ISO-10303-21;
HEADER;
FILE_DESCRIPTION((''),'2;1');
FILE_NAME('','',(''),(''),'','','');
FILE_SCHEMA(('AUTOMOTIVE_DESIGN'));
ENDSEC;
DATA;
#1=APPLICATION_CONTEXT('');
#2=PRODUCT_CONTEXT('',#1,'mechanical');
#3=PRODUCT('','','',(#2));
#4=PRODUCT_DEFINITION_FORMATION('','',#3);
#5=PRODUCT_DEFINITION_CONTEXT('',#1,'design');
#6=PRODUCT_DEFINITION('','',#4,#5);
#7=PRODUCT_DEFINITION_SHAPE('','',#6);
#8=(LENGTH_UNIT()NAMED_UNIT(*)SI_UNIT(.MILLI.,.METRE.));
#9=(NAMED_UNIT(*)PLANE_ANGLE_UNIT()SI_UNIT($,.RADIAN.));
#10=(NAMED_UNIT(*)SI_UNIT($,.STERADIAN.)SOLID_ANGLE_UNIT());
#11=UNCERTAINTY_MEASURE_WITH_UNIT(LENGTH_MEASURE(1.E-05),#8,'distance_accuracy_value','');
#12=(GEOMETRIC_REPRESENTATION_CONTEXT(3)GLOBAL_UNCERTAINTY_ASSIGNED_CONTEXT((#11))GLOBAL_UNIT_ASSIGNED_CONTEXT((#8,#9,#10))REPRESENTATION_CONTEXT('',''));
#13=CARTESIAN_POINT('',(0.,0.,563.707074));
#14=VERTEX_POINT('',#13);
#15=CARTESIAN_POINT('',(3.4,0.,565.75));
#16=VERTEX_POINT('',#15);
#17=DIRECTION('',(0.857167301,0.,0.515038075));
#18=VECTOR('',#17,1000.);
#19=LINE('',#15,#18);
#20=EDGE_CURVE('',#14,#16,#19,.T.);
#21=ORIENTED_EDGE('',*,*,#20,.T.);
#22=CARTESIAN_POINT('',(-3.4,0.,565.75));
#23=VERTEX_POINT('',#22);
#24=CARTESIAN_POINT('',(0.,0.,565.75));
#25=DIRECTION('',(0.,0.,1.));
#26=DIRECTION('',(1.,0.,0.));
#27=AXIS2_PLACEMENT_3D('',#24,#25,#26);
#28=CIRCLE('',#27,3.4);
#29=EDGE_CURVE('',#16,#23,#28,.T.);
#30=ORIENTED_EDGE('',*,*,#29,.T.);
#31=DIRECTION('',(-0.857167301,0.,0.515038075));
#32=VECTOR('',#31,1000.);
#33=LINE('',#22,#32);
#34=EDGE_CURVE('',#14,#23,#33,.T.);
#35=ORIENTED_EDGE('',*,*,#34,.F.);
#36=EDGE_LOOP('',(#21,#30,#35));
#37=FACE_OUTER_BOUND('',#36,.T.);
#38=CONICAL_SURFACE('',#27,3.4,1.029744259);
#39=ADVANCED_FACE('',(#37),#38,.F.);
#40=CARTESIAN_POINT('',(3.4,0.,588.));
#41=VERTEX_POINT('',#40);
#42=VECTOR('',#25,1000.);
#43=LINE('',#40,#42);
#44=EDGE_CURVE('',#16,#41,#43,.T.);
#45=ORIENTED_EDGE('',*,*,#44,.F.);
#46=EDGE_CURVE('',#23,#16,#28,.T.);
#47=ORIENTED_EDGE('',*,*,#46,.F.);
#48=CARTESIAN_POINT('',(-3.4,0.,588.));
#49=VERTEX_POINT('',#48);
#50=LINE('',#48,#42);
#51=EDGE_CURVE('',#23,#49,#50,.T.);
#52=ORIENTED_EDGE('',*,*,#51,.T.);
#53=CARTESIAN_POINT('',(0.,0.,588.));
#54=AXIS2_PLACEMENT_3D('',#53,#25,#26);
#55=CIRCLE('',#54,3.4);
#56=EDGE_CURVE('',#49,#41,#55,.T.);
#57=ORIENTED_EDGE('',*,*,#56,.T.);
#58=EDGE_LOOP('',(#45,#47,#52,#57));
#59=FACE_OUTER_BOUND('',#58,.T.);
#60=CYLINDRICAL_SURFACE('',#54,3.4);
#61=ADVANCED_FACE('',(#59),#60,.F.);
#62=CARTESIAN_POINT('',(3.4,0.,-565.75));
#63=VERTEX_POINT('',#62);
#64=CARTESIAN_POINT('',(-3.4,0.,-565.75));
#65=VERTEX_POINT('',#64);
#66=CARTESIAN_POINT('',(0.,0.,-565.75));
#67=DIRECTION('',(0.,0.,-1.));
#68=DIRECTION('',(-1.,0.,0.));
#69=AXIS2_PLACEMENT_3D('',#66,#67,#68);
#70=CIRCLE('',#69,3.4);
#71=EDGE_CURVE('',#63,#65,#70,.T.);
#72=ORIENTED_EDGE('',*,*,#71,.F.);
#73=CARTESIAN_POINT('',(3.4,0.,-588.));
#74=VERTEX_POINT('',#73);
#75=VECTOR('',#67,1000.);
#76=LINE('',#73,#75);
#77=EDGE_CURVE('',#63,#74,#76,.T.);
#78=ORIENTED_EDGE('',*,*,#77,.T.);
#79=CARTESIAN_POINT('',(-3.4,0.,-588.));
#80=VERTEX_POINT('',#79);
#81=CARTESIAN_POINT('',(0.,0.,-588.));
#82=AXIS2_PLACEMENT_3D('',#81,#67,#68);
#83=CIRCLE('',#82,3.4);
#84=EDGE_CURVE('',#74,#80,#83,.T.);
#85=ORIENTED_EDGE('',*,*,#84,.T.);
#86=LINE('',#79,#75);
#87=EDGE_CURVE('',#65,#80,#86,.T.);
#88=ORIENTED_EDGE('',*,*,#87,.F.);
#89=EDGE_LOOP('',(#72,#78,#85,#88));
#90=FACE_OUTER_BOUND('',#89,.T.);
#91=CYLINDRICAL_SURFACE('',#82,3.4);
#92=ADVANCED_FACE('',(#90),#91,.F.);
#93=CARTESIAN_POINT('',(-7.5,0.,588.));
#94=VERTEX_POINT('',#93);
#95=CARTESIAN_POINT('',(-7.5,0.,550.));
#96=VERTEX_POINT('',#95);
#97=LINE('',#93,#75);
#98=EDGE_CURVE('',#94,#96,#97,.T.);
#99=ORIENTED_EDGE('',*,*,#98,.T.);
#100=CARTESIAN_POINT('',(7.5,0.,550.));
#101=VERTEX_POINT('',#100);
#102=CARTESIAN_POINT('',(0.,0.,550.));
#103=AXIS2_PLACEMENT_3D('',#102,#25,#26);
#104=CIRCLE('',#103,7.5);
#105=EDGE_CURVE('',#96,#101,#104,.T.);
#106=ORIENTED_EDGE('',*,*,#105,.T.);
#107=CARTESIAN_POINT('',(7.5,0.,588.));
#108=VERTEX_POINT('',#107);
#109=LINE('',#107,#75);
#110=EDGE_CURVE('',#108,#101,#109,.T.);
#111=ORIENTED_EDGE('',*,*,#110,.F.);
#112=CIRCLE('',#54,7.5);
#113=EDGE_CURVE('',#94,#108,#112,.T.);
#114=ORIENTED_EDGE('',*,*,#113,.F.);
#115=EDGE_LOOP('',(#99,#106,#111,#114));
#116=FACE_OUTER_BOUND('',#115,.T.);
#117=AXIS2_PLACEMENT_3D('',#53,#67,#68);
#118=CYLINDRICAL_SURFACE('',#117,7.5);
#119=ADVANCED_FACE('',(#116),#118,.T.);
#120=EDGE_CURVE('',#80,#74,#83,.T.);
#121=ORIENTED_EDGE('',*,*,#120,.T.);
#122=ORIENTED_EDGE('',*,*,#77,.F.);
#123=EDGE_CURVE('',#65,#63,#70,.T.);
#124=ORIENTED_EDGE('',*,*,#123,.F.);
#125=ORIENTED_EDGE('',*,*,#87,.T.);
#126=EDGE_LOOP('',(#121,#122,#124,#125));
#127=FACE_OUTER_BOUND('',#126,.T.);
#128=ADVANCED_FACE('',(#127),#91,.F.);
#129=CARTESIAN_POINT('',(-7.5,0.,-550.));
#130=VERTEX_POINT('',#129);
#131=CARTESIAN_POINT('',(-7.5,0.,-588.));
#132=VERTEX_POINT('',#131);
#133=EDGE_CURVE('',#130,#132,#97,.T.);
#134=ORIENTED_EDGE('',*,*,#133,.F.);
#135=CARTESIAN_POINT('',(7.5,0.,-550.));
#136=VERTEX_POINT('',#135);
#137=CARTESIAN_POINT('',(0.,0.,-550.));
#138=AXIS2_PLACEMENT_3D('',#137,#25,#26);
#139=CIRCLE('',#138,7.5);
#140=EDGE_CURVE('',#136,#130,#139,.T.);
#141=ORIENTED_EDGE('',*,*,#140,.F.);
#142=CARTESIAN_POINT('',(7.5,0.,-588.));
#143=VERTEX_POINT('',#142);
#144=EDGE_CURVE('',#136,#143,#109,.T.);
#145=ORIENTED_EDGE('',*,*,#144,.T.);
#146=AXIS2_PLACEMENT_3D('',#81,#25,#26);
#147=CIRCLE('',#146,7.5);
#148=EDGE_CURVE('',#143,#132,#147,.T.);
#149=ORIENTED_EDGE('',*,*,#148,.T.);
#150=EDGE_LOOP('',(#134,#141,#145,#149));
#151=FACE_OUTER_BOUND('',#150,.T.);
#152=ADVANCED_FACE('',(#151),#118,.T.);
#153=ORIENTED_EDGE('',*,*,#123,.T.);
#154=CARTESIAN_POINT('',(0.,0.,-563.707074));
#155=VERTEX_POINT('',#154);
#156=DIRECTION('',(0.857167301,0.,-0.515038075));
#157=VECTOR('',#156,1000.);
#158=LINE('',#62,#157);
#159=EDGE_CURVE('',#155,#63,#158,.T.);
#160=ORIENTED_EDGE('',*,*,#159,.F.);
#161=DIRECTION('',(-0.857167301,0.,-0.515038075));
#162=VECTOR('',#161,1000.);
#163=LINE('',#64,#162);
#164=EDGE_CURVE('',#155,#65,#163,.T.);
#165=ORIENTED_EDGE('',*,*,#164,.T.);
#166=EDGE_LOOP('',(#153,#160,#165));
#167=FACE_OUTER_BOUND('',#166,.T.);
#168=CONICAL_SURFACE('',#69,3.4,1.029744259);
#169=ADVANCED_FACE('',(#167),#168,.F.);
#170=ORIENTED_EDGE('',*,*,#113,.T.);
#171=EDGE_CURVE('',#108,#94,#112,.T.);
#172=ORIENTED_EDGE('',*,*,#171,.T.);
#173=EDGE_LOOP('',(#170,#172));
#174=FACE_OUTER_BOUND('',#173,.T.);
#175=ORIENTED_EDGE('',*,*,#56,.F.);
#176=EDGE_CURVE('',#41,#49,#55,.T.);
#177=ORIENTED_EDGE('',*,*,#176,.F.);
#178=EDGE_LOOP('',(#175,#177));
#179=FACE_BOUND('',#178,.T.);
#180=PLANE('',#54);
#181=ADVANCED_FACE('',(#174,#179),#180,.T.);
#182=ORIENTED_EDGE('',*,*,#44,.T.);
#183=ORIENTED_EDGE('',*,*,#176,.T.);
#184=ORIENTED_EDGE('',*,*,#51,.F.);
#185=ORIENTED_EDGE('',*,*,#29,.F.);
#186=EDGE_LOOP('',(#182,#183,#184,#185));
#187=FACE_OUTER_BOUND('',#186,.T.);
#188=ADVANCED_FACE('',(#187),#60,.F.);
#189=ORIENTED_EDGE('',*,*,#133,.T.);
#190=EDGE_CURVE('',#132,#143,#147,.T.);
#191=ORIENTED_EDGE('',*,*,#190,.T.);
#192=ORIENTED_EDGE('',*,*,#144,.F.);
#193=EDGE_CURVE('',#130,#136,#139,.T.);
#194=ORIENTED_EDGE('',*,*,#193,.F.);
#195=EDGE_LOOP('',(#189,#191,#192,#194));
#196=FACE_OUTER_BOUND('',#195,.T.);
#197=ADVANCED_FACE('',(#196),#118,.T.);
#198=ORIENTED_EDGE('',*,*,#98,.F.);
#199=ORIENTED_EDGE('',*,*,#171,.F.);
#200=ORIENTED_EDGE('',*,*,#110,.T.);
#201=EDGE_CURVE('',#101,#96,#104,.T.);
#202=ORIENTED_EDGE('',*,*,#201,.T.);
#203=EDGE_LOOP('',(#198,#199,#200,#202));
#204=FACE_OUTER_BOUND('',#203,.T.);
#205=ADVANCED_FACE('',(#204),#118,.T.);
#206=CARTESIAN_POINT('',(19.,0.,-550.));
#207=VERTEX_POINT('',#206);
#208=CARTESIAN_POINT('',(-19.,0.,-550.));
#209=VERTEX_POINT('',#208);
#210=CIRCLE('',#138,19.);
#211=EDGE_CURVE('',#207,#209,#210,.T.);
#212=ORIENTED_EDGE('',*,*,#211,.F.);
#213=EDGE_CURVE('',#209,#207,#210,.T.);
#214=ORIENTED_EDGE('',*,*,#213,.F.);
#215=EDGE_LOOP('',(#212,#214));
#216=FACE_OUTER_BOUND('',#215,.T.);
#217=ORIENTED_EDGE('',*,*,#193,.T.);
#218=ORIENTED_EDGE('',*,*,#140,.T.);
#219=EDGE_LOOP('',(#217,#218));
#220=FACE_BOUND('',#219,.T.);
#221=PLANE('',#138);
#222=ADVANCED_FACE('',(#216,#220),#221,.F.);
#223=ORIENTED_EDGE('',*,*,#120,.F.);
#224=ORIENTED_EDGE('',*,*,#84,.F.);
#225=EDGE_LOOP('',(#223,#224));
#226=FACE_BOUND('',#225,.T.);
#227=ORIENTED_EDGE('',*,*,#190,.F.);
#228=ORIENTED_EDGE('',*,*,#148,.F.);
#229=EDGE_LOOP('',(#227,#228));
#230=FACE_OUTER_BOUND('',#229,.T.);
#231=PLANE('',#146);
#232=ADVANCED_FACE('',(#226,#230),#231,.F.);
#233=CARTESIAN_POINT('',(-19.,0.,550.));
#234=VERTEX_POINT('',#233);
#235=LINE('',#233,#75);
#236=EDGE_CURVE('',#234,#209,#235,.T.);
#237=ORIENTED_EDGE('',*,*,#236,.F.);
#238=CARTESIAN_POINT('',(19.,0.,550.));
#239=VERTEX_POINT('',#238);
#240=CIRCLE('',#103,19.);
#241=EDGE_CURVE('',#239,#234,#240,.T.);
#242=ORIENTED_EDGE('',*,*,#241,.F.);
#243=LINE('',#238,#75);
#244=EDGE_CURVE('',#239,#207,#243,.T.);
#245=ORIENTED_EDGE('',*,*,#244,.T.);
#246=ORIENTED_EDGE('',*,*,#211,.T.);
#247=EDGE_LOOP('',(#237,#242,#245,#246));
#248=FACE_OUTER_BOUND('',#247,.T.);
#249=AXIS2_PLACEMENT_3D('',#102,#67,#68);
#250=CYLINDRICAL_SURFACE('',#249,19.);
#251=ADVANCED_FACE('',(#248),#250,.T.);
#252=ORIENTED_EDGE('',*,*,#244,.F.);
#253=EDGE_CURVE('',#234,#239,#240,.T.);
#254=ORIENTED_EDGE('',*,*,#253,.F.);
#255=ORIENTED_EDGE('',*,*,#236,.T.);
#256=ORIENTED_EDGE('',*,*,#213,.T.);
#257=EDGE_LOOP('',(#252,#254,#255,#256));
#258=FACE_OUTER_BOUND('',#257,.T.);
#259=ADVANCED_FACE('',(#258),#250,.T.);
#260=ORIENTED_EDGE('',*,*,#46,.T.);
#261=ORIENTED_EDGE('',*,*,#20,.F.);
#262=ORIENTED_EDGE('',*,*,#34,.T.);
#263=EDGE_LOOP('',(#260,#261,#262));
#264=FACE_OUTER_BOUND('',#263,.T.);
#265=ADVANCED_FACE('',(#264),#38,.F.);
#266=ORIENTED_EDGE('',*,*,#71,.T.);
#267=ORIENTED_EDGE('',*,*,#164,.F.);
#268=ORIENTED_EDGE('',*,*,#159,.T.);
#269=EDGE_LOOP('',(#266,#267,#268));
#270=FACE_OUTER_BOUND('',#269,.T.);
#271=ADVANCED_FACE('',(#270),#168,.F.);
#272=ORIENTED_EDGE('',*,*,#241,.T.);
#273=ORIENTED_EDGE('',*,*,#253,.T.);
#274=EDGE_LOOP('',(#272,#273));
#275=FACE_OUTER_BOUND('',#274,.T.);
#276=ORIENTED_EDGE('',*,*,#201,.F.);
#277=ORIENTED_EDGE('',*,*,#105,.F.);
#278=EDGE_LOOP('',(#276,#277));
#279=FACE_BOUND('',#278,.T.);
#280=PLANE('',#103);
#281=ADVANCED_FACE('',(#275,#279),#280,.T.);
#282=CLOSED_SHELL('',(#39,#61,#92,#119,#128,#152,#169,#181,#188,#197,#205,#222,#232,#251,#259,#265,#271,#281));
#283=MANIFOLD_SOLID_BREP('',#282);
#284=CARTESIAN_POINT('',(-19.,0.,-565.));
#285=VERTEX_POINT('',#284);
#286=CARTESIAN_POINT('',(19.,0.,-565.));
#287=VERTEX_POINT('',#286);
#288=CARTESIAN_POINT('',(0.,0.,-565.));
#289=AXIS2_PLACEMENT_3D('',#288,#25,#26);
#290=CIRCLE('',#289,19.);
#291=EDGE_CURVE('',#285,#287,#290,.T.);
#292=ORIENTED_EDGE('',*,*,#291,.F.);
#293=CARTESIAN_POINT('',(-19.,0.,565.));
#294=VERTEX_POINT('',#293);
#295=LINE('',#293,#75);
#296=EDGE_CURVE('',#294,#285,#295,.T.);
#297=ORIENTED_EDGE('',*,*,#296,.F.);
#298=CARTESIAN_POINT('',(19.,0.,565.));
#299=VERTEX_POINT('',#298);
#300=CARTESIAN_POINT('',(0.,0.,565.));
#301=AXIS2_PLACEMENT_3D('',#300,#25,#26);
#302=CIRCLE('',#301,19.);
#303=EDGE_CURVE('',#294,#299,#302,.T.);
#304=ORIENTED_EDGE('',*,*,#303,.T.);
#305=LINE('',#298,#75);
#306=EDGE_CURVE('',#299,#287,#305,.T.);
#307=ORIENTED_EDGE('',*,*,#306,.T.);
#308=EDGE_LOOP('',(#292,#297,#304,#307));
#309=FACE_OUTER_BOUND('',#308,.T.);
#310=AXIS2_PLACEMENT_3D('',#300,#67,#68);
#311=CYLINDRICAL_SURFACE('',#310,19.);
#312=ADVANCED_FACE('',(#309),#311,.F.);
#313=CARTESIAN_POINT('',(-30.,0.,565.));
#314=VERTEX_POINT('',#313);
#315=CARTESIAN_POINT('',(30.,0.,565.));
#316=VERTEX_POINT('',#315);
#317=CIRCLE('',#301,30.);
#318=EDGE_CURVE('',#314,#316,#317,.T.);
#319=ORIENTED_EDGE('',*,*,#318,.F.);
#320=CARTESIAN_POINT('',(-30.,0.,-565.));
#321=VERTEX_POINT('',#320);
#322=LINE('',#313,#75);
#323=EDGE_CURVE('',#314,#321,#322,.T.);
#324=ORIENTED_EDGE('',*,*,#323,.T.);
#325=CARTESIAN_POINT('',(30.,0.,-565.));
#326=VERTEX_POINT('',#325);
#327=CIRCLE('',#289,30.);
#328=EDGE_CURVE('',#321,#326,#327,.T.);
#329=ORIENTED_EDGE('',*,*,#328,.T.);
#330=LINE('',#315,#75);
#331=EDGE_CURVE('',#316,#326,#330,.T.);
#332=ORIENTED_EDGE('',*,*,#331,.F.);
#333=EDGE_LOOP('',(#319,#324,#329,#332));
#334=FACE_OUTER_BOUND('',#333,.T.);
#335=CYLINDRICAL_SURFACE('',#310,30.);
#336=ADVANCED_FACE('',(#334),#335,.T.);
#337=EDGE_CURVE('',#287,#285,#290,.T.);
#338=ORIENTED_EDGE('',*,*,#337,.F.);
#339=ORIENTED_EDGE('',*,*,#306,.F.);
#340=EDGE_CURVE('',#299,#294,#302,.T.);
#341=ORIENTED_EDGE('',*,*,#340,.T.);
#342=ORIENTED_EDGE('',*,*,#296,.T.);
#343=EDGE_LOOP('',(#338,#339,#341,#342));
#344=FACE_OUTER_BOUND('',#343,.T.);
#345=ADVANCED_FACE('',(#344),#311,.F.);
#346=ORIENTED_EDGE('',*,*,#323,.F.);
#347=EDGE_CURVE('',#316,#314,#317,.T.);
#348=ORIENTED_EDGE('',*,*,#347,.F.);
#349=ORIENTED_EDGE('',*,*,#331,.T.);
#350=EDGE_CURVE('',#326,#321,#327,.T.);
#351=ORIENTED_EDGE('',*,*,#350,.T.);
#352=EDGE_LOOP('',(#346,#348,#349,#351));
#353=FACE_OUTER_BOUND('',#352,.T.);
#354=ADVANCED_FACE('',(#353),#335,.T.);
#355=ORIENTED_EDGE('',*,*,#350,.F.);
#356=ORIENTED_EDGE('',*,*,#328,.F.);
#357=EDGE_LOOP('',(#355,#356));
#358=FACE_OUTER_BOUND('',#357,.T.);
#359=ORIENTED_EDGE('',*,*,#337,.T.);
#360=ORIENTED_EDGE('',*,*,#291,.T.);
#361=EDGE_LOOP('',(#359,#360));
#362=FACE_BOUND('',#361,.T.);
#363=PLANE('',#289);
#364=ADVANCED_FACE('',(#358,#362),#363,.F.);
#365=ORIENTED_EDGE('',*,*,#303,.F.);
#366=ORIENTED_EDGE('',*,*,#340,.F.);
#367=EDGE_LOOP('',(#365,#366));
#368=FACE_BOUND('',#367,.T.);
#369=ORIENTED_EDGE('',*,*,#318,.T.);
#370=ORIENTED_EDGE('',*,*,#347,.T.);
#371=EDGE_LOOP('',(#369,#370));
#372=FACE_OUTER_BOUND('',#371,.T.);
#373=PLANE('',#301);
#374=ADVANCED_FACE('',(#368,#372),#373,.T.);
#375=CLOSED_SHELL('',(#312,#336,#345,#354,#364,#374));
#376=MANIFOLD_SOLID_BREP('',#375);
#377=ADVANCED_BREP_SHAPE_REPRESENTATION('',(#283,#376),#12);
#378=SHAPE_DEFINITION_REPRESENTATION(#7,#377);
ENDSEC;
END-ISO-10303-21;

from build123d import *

# Parameters (mm, degrees)
SKETCH_1_R      = 7.5
EXTRUDE_1_DEPTH = 588
SKETCH_2_R      = 19
EXTRUDE_2_DEPTH = 550
SKETCH_3_R      = 30
SKETCH_3_R_2    = 19
EXTRUDE_3_DEPTH = 565


with BuildPart() as part:
    # 草图1 → 凸台-拉伸1 (new, symmetric)
    with BuildSketch(Plane.XY):
        Circle(SKETCH_1_R)
    extrude(amount=EXTRUDE_1_DEPTH, both=True)

    # 草图2 → 凸台-拉伸2 (add, symmetric)
    with BuildSketch(Plane.XY):
        Circle(SKETCH_2_R)
    extrude(amount=EXTRUDE_2_DEPTH, both=True)

    # 草图5 → M8 螺纹孔1 (revolve, cut)
    with BuildSketch(Plane(origin=(0, 0, -588), x_dir=(0, 1, 0), z_dir=(1, 0, 0))):
        Polygon((0, 0), (0, 24.292926105), (3.4, 22.25), (3.4, 0), align=None)
    revolve(axis=Axis((0, 0, -594.35), (0, 0, 1)), mode=Mode.SUBTRACT)

    # 草图8 → M8 螺纹孔2 (revolve, cut)
    with BuildSketch(Plane(origin=(0, 0, 588), x_dir=(0, -1, 0), z_dir=(1, 0, 0))):
        Polygon((0, 0), (0, 24.292926105), (3.4, 22.25), (3.4, 0), align=None)
    revolve(axis=Axis((0, 0, 594.35), (0, 0, -1)), mode=Mode.SUBTRACT)


with BuildPart() as body_2:
    # 草图3 → 凸台-拉伸3 (new, symmetric)
    with BuildSketch(Plane.XY):
        Circle(SKETCH_3_R)
        Circle(SKETCH_3_R_2, mode=Mode.SUBTRACT)
    extrude(amount=EXTRUDE_3_DEPTH, both=True)


solid = Compound([part.part, body_2.part])
